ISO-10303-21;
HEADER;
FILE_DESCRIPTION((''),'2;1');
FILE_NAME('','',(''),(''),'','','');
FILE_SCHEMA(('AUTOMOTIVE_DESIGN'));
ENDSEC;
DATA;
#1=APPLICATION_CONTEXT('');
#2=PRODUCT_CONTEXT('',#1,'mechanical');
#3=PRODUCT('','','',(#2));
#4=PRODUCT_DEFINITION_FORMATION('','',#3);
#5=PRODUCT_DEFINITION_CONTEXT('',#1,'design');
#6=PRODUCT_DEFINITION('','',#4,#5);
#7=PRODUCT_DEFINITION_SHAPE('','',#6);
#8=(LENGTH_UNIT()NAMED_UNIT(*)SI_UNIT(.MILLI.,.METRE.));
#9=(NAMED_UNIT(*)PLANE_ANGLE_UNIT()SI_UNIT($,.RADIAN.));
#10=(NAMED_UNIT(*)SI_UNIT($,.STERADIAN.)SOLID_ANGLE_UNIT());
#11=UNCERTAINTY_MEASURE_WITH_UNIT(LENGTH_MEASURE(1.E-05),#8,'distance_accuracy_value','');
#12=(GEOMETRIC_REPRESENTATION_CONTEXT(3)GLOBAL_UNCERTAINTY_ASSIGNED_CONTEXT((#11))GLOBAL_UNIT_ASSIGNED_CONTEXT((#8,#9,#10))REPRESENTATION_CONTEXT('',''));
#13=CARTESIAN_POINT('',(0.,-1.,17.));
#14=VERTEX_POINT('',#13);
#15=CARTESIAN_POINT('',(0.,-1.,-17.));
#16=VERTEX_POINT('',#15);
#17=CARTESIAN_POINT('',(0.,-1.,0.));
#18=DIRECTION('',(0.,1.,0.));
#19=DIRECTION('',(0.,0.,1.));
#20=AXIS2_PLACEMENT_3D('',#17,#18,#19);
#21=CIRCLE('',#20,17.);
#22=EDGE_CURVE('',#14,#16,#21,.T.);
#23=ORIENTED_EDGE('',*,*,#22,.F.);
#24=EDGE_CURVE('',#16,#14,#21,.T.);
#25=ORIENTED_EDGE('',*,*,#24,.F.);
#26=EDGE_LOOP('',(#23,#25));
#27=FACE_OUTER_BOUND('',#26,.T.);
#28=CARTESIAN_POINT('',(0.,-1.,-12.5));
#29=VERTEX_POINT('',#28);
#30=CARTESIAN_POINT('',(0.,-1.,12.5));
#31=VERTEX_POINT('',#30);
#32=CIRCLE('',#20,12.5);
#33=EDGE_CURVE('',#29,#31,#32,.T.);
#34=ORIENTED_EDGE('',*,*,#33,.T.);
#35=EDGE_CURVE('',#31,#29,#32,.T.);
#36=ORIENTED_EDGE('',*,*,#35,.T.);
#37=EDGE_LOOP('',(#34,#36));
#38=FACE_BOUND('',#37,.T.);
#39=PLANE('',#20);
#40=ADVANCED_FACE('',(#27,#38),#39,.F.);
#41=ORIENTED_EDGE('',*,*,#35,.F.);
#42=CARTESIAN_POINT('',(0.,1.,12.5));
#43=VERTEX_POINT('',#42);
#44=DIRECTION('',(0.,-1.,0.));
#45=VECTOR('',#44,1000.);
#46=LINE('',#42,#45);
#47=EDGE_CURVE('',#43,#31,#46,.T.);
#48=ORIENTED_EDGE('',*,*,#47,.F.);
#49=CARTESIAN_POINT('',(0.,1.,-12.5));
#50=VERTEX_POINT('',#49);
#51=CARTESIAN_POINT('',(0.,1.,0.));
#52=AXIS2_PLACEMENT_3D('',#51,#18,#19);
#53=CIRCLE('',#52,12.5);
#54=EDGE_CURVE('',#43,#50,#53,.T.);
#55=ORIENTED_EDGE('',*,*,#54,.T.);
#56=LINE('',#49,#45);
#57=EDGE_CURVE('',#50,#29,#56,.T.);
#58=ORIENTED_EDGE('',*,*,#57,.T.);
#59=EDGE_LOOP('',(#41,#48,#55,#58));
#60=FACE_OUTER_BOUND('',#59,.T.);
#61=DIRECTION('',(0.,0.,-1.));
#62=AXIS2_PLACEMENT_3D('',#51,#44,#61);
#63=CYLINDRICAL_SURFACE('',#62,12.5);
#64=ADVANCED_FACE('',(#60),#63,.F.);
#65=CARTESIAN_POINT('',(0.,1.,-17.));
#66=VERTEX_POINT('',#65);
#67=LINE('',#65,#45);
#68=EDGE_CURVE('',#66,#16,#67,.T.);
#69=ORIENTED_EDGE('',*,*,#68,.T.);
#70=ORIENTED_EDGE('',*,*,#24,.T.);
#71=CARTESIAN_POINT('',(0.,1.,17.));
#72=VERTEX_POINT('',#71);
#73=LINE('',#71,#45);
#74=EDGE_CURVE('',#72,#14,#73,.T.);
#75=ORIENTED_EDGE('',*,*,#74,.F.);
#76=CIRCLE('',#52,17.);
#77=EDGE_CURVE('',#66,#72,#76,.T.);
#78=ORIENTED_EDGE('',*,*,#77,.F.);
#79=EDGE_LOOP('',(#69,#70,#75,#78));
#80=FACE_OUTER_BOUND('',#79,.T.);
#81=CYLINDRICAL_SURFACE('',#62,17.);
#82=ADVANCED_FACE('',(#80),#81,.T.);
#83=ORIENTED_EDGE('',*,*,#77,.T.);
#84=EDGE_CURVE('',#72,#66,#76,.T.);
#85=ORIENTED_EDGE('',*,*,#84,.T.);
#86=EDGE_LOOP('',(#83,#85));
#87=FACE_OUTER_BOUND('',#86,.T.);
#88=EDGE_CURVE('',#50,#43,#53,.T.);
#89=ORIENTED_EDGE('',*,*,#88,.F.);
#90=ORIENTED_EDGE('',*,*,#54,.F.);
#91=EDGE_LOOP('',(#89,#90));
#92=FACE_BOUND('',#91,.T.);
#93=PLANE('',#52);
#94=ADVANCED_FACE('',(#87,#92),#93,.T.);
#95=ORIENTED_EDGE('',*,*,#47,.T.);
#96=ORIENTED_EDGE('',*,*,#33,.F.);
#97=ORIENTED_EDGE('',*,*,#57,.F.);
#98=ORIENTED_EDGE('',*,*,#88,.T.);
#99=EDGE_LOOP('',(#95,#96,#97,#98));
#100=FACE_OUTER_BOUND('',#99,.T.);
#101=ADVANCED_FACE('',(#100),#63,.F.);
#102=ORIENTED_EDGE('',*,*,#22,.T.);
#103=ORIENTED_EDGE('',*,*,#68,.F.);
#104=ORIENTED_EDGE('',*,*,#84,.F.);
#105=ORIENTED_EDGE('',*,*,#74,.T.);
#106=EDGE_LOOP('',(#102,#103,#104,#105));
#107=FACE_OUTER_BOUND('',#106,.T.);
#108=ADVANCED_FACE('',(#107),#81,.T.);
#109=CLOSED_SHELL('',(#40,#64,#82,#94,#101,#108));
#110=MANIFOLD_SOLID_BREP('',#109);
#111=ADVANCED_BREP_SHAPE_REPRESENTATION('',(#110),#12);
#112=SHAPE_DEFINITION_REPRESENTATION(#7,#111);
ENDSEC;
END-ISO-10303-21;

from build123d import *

# Parameters (mm, degrees)
SKETCH_1_R      = 17
SKETCH_1_R_2    = 12.5
EXTRUDE_1_DEPTH = 1


with BuildPart() as part:
    # 草图1 → 凸台-拉伸1 (new, symmetric)
    with BuildSketch(Plane(origin=(0, 0, 0), x_dir=(1, 0, 0), z_dir=(0, 1, 0))):
        with Locations(Location((0, 0, 0), (0, 0, 270))):
            Circle(SKETCH_1_R)
        with Locations(Location((0, 0, 0), (0, 0, 270))):
            Circle(SKETCH_1_R_2, mode=Mode.SUBTRACT)
    extrude(amount=EXTRUDE_1_DEPTH, both=True)


solid = part.part
